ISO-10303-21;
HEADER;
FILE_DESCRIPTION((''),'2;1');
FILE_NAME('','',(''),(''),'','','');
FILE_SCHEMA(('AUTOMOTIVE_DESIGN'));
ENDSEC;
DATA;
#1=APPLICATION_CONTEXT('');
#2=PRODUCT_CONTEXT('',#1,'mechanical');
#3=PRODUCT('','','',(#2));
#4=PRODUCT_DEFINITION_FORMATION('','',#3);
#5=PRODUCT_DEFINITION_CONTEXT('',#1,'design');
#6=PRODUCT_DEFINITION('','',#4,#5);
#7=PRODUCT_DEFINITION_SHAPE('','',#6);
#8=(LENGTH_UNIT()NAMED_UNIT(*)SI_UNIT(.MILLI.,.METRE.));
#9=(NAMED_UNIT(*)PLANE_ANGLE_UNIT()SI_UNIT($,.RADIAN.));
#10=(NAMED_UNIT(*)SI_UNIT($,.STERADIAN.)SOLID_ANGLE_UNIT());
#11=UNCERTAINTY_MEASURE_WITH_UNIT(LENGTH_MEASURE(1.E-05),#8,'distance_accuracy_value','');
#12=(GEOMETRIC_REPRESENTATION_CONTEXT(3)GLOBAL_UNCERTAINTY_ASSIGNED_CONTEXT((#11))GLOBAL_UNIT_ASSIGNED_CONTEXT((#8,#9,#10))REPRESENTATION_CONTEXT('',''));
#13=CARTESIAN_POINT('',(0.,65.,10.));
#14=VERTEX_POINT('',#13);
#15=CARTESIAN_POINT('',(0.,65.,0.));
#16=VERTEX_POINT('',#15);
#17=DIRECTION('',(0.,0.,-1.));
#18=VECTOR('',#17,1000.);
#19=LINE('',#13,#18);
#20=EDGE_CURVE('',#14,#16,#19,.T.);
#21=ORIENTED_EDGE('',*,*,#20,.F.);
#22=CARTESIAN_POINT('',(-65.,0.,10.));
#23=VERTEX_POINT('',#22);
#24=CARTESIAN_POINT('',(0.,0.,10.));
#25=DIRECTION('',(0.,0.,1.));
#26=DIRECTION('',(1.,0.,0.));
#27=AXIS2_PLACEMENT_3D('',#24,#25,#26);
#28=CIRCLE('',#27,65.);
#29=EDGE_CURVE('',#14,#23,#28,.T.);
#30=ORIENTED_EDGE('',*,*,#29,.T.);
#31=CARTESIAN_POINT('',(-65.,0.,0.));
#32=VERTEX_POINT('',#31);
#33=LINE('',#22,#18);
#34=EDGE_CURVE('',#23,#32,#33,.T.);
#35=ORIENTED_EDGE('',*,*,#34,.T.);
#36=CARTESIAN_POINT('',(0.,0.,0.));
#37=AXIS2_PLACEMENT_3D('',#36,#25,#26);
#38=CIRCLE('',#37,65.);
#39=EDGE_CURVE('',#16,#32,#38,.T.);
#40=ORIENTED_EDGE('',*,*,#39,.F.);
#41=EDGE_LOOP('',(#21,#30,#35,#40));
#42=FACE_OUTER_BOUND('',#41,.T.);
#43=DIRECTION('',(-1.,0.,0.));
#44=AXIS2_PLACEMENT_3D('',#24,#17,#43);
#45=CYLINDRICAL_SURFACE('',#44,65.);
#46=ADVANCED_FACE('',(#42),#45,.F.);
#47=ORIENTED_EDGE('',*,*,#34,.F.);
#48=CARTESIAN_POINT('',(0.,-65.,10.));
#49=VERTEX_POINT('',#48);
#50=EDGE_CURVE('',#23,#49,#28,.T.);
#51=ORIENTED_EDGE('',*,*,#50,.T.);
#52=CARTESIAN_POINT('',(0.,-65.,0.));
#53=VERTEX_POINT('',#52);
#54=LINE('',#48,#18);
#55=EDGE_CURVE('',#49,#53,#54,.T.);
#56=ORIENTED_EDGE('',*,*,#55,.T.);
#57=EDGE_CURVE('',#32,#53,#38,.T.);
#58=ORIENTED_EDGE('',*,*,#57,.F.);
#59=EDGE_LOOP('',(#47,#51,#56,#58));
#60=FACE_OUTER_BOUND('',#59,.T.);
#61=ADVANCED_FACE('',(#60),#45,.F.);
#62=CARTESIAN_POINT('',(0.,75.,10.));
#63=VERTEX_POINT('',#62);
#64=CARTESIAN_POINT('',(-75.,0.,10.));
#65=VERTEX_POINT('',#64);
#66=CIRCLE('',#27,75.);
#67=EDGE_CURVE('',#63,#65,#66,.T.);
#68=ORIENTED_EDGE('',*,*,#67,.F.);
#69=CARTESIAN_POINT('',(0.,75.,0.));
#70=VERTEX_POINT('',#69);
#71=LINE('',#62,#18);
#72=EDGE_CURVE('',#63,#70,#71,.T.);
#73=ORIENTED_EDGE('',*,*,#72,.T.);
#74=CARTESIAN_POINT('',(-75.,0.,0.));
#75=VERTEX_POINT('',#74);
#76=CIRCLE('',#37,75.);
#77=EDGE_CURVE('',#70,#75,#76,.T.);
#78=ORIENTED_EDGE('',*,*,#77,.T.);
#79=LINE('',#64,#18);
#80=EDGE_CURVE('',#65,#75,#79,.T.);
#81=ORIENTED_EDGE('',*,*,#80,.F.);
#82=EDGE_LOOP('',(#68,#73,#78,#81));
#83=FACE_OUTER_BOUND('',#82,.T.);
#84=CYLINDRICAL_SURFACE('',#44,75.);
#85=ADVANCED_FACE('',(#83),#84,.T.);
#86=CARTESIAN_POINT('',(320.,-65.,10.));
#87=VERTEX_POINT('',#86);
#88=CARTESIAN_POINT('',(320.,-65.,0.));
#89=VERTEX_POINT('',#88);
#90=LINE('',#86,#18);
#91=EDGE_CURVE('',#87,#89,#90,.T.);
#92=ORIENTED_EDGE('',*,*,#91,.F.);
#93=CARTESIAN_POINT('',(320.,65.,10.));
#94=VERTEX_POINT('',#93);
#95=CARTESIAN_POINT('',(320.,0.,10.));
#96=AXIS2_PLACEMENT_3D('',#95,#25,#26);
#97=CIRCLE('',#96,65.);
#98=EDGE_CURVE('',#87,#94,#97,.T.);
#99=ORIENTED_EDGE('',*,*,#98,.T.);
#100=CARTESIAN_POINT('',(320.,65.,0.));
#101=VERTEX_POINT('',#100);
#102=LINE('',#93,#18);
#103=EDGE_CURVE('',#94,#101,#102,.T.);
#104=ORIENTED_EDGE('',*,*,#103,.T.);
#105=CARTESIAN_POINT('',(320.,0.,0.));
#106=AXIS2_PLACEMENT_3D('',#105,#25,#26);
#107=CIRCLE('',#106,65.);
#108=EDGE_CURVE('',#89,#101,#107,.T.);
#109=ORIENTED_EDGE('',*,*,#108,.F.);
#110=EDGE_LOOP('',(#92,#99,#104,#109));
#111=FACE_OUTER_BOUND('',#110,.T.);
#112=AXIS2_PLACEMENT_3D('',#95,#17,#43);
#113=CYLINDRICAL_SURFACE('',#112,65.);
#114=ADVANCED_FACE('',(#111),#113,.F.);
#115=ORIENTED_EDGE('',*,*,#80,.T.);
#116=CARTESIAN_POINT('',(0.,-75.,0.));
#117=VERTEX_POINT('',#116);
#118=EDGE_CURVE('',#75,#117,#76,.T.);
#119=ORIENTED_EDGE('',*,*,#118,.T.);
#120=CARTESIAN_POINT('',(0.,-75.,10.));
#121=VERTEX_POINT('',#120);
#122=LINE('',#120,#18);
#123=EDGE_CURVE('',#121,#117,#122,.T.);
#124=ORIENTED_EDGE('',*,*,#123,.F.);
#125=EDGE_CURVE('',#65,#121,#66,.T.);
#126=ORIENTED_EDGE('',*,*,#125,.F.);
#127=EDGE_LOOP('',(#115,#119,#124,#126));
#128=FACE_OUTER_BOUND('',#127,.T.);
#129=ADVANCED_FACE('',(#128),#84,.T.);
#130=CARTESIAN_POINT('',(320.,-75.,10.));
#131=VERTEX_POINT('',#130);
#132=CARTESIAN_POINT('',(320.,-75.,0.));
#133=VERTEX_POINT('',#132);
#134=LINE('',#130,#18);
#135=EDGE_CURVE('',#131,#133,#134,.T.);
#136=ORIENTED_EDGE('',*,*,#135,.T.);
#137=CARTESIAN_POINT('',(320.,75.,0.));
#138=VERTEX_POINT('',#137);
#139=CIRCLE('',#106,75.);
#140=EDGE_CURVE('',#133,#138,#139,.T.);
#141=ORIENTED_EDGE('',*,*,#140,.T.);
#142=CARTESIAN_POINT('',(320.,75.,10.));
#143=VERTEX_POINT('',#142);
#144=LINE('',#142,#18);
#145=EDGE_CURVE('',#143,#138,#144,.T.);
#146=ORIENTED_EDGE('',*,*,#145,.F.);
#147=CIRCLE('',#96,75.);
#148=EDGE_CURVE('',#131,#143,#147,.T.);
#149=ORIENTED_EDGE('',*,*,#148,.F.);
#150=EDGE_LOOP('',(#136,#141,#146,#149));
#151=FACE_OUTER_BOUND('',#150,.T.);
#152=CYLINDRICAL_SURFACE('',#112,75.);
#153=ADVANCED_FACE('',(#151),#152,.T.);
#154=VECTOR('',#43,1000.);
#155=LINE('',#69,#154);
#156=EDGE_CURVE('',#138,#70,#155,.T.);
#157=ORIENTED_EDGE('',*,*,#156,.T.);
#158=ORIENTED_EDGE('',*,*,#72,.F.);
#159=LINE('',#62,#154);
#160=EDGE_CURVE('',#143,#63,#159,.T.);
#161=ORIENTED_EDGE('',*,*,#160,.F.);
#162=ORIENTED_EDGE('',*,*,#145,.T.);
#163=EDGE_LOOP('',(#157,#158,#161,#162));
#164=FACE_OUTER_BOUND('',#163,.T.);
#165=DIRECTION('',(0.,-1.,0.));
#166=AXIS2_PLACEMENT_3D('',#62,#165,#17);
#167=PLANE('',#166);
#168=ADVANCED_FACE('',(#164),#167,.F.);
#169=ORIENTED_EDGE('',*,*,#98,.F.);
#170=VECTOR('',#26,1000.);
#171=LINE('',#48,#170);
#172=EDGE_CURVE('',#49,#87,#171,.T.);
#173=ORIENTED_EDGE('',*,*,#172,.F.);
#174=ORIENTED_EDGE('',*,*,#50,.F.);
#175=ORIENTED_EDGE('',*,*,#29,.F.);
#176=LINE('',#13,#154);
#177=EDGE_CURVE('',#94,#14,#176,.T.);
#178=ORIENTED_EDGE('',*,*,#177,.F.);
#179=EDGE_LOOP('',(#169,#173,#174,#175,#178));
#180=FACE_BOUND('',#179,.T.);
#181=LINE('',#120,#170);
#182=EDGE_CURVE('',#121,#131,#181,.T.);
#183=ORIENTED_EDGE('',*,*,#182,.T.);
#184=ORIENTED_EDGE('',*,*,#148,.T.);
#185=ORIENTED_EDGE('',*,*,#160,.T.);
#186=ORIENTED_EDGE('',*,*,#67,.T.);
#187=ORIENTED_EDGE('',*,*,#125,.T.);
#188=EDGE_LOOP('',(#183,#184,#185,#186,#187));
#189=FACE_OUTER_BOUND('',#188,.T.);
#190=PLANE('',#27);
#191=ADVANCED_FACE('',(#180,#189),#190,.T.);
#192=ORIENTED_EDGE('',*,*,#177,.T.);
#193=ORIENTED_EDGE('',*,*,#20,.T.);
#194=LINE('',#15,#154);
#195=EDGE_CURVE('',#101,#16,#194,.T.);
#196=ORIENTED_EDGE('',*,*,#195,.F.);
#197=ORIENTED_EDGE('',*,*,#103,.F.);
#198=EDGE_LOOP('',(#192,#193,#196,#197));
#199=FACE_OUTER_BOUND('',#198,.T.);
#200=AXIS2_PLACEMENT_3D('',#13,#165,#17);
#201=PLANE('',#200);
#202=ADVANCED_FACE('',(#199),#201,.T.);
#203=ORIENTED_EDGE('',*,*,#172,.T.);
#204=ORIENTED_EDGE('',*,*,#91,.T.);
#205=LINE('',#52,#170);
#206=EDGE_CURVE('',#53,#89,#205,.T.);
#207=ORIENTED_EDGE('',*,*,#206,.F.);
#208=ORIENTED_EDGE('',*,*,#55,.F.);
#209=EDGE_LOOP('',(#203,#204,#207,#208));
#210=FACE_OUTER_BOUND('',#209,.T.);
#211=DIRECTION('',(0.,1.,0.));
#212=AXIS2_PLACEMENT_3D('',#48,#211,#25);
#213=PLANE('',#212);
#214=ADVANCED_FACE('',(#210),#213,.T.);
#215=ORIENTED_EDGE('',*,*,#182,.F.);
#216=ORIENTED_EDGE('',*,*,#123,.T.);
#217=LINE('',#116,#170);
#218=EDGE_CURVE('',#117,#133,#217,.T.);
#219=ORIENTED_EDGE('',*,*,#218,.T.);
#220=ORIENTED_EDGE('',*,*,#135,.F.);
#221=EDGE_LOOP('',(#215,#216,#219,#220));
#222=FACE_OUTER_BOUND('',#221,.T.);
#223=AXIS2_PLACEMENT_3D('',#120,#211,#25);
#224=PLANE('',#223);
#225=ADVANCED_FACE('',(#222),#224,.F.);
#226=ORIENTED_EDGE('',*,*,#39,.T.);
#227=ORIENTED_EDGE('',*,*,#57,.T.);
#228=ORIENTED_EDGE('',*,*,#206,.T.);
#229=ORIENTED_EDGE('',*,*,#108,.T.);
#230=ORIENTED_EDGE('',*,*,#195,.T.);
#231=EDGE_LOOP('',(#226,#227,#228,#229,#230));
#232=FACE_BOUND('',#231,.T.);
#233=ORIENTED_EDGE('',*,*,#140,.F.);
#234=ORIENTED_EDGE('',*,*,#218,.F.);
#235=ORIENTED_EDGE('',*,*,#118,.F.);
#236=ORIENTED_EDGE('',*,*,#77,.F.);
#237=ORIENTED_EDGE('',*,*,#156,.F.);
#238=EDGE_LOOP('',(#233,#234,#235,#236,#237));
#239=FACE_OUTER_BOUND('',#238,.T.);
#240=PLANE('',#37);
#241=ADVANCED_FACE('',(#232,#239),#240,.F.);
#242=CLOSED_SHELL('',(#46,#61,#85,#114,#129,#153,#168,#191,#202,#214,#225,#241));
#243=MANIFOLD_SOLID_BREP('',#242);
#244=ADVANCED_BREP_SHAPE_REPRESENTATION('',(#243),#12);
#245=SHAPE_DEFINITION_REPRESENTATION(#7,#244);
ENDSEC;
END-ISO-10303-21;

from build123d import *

# Parameters (mm, degrees)
EXTRUDE_1_DEPTH = 10


with BuildPart() as part:
    # 草图1 → 凸台-拉伸1 (new body)
    with BuildSketch(Plane.XY):
        with BuildLine():
            Line((0, 75), (320, 75))
            ThreePointArc((320, 75), (395, 0), (320, -75))
            Line((320, -75), (0, -75))
            ThreePointArc((0, -75), (-75, 0), (0, 75))
        make_face()
        with BuildLine():
            Line((0, 65), (320, 65))
            ThreePointArc((320, 65), (385, 0), (320, -65))
            Line((320, -65), (0, -65))
            ThreePointArc((0, -65), (-65, 0), (0, 65))
        make_face(mode=Mode.SUBTRACT)
    extrude(amount=EXTRUDE_1_DEPTH)


solid = part.part
